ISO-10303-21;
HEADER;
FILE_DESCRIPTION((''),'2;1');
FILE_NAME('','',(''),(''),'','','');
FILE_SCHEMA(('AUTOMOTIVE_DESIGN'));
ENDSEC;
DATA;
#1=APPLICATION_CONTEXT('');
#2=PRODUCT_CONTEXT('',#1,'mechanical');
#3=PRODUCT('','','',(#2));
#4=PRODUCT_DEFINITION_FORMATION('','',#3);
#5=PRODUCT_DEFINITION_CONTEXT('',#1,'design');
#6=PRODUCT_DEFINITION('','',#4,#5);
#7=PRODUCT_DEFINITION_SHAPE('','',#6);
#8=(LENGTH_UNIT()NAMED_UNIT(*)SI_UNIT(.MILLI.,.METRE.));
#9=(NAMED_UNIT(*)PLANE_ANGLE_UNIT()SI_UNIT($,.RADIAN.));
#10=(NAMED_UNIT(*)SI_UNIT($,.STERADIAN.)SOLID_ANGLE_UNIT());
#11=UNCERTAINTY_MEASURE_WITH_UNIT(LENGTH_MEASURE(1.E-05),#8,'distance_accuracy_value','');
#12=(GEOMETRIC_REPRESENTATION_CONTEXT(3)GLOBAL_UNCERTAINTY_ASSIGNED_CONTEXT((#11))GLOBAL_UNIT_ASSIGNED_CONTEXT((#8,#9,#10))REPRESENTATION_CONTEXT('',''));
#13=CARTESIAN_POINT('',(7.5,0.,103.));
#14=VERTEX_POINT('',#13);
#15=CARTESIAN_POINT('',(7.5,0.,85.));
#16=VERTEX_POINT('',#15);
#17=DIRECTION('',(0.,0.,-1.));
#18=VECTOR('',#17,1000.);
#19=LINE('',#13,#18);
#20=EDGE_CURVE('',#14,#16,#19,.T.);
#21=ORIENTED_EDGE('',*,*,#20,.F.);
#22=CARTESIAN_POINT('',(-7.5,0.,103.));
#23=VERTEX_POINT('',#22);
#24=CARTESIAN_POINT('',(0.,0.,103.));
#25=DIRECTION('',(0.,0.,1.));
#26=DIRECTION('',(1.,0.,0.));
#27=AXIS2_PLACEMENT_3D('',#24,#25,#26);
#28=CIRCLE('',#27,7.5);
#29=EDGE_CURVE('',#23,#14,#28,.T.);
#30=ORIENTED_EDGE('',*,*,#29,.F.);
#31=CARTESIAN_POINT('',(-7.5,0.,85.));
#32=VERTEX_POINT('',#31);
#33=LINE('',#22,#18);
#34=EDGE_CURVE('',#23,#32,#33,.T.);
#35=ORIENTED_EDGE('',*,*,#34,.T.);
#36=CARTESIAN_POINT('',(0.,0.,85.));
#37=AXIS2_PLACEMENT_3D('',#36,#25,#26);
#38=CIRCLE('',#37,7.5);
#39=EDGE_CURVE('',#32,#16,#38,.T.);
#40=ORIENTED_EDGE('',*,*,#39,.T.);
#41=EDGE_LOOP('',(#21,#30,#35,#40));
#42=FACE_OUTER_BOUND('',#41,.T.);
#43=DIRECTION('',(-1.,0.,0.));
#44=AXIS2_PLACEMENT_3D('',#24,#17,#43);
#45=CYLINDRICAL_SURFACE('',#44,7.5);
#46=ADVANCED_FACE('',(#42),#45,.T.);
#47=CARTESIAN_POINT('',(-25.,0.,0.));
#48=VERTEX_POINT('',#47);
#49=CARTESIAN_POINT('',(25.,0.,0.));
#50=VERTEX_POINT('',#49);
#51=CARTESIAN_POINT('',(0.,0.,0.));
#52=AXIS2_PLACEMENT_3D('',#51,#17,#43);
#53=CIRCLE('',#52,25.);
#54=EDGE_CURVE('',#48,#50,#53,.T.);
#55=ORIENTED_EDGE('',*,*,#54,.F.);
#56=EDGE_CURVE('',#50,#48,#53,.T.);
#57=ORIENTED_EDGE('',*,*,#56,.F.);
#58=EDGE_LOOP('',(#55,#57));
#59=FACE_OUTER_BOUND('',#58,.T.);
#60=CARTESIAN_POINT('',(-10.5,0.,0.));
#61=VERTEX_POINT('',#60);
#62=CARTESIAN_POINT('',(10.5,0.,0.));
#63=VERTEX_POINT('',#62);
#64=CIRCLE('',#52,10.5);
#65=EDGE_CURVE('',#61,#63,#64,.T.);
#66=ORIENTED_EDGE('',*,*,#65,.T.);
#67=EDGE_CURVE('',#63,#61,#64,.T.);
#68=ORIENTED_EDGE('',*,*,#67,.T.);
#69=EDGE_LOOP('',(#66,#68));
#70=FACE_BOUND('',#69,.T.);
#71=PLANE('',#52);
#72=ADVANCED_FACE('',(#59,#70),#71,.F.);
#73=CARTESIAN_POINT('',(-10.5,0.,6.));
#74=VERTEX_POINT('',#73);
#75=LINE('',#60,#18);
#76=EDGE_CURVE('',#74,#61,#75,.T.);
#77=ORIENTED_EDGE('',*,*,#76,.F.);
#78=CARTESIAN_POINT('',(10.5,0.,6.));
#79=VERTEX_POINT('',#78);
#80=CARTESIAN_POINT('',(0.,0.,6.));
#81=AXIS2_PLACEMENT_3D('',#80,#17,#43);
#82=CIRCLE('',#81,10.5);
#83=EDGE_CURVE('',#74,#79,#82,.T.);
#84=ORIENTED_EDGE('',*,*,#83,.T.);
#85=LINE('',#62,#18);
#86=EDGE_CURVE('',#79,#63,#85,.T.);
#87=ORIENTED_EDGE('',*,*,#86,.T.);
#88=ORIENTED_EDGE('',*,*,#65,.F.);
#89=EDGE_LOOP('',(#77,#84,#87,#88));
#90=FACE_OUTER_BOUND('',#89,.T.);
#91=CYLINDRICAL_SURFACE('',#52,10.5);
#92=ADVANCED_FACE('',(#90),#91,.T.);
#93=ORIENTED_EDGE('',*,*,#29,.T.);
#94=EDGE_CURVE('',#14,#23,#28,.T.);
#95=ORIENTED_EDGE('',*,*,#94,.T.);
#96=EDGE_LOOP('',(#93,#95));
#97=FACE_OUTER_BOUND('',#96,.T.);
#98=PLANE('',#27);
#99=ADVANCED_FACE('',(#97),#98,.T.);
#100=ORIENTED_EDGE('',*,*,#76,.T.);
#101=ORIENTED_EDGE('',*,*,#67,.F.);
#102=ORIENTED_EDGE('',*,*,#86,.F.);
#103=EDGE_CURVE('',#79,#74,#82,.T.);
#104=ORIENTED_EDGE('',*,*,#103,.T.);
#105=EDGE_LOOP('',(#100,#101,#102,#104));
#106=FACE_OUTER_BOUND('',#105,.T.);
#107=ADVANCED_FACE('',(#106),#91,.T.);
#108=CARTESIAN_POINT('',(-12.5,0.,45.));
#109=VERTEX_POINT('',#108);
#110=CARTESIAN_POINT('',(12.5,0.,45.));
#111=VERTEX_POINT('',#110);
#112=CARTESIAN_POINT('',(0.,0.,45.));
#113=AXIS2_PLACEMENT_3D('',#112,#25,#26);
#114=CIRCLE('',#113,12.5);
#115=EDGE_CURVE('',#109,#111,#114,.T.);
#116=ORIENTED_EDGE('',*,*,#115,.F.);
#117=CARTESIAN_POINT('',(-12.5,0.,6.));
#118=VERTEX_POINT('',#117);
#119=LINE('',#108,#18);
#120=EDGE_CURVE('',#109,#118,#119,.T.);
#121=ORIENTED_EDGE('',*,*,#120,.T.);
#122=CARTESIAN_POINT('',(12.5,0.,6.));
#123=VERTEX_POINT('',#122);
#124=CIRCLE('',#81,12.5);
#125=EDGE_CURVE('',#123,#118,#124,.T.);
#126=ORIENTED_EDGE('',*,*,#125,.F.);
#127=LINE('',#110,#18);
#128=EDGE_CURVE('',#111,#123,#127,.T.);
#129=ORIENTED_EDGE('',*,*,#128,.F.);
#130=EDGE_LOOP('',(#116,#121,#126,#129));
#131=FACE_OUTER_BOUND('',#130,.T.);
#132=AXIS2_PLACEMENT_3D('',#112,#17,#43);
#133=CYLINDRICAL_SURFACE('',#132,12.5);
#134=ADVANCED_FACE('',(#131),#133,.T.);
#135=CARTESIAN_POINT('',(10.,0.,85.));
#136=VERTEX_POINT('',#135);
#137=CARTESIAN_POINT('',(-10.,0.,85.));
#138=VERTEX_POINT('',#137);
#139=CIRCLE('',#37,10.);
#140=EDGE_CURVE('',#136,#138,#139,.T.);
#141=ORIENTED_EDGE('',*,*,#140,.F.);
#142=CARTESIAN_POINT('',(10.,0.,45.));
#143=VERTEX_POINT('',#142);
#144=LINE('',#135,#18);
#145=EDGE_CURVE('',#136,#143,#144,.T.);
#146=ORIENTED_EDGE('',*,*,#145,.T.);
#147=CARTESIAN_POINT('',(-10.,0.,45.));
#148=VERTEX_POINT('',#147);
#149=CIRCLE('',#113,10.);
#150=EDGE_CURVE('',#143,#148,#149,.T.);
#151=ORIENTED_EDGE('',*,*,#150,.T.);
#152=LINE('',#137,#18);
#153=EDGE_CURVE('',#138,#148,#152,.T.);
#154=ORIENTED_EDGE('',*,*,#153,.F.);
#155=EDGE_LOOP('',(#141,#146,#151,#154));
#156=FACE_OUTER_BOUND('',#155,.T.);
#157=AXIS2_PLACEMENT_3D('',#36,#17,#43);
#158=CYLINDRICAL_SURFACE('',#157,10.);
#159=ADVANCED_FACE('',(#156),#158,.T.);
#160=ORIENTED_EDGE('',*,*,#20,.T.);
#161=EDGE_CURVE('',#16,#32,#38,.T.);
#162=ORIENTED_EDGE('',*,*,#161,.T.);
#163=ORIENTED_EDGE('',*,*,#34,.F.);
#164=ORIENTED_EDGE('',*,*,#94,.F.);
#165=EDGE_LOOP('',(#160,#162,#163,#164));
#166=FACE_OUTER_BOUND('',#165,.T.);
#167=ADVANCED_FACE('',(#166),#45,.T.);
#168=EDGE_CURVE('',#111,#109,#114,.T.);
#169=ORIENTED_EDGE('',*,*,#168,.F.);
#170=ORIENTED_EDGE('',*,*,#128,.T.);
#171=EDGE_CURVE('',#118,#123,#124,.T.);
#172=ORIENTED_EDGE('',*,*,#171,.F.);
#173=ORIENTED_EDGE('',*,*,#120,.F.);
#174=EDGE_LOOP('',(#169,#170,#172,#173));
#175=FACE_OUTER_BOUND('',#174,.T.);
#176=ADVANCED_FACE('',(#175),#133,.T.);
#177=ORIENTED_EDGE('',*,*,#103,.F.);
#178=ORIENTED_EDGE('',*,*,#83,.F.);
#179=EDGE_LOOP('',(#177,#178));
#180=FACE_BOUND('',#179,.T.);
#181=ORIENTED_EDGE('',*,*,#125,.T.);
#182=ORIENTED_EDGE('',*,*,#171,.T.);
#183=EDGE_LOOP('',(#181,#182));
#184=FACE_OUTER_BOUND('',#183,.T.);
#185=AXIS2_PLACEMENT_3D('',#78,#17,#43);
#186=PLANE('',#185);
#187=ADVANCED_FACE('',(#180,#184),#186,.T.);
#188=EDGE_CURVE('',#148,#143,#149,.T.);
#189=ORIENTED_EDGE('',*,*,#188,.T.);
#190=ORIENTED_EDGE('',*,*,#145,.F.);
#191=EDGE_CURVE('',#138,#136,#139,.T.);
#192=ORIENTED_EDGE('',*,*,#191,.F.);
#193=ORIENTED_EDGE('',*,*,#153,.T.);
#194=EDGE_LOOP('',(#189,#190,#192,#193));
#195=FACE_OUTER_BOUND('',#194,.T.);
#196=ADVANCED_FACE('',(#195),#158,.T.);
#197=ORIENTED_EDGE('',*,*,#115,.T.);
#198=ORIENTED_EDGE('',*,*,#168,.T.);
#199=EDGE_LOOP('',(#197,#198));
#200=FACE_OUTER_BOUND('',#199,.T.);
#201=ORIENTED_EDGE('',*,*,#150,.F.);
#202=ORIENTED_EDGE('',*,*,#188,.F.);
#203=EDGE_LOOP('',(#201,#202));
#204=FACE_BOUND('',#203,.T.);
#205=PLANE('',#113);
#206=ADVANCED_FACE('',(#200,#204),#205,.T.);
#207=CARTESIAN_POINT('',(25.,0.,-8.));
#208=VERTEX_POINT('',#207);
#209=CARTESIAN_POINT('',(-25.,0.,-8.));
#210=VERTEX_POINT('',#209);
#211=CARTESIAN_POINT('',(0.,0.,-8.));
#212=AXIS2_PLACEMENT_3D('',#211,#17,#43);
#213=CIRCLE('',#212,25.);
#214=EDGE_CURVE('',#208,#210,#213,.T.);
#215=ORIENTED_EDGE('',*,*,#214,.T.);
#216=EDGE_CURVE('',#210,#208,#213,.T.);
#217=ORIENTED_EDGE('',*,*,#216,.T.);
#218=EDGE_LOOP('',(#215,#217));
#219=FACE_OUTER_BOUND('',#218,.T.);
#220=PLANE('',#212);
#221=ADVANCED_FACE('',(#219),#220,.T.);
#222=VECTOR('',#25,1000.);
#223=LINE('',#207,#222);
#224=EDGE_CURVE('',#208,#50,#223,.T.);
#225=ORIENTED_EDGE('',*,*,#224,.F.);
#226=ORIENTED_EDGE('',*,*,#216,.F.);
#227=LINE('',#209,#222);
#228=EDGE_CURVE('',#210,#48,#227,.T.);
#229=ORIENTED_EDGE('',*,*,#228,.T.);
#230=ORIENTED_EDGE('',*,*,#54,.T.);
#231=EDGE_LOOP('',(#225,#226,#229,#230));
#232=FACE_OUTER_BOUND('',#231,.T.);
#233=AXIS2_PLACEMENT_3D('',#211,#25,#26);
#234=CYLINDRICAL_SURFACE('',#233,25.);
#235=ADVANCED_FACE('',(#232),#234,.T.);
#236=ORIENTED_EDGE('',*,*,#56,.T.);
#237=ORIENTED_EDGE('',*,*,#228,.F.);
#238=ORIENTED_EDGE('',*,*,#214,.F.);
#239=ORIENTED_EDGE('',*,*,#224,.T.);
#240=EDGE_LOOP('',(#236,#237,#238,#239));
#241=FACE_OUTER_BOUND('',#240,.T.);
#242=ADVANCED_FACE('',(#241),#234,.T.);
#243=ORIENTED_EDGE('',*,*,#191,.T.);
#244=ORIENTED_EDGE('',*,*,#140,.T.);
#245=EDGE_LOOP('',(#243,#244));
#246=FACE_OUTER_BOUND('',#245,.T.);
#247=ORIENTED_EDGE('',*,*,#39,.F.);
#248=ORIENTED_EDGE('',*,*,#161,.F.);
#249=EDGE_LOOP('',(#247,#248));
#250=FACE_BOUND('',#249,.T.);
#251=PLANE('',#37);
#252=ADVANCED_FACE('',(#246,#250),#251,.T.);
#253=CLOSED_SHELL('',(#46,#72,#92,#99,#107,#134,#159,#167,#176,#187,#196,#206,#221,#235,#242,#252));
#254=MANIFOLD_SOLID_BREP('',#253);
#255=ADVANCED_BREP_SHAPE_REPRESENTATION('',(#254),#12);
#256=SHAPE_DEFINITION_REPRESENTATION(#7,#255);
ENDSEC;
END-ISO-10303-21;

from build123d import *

# Parameters (mm, degrees)
SKETCH_1_R      = 12.5
EXTRUDE_1_DEPTH = 45
SKETCH_2_R      = 25
EXTRUDE_2_DEPTH = 8
SKETCH_3_R      = 10
EXTRUDE_3_DEPTH = 40
SKETCH_5_W      = 2
SKETCH_5_H      = 6
SKETCH_6_R      = 7.5
EXTRUDE_4_DEPTH = 18


with BuildPart() as part:
    # 草图1 → 凸台-拉伸1 (new body)
    with BuildSketch(Plane.XY):
        with Locations(Location((0, 0, 0), (0, 0, 180))):
            Circle(SKETCH_1_R)
    extrude(amount=EXTRUDE_1_DEPTH)

    # 草图2 → 凸台-拉伸2 (add)
    with BuildSketch(Plane(origin=(0, 0, 0), x_dir=(-1, 0, 0), z_dir=(0, 0, -1))):
        Circle(SKETCH_2_R)
    extrude(amount=EXTRUDE_2_DEPTH)

    # 草图3 → 凸台-拉伸3 (add)
    with BuildSketch(Plane.XY.offset(45)):
        Circle(SKETCH_3_R)
    extrude(amount=EXTRUDE_3_DEPTH)

    # 草图5 → 切除-旋转1 (revolve, cut)
    with BuildSketch(Plane(origin=(0, 0, 0), x_dir=(1, 0, 0), z_dir=(0, 1, 0)), mode=Mode.PRIVATE) as cut_revolve_1_sk:
        with Locations((11.5, -3)):
            Rectangle(SKETCH_5_W, SKETCH_5_H)
    revolve(cut_revolve_1_sk.sketch.rotate(Axis((0, 0, 0), (0, 0, 1)), 180), axis=Axis((0, 0, 0), (0, 0, 1)), mode=Mode.SUBTRACT)

    # 草图6 → 凸台-拉伸4 (add)
    with BuildSketch(Plane.XY.offset(85)):
        Circle(SKETCH_6_R)
    extrude(amount=EXTRUDE_4_DEPTH)


solid = part.part
